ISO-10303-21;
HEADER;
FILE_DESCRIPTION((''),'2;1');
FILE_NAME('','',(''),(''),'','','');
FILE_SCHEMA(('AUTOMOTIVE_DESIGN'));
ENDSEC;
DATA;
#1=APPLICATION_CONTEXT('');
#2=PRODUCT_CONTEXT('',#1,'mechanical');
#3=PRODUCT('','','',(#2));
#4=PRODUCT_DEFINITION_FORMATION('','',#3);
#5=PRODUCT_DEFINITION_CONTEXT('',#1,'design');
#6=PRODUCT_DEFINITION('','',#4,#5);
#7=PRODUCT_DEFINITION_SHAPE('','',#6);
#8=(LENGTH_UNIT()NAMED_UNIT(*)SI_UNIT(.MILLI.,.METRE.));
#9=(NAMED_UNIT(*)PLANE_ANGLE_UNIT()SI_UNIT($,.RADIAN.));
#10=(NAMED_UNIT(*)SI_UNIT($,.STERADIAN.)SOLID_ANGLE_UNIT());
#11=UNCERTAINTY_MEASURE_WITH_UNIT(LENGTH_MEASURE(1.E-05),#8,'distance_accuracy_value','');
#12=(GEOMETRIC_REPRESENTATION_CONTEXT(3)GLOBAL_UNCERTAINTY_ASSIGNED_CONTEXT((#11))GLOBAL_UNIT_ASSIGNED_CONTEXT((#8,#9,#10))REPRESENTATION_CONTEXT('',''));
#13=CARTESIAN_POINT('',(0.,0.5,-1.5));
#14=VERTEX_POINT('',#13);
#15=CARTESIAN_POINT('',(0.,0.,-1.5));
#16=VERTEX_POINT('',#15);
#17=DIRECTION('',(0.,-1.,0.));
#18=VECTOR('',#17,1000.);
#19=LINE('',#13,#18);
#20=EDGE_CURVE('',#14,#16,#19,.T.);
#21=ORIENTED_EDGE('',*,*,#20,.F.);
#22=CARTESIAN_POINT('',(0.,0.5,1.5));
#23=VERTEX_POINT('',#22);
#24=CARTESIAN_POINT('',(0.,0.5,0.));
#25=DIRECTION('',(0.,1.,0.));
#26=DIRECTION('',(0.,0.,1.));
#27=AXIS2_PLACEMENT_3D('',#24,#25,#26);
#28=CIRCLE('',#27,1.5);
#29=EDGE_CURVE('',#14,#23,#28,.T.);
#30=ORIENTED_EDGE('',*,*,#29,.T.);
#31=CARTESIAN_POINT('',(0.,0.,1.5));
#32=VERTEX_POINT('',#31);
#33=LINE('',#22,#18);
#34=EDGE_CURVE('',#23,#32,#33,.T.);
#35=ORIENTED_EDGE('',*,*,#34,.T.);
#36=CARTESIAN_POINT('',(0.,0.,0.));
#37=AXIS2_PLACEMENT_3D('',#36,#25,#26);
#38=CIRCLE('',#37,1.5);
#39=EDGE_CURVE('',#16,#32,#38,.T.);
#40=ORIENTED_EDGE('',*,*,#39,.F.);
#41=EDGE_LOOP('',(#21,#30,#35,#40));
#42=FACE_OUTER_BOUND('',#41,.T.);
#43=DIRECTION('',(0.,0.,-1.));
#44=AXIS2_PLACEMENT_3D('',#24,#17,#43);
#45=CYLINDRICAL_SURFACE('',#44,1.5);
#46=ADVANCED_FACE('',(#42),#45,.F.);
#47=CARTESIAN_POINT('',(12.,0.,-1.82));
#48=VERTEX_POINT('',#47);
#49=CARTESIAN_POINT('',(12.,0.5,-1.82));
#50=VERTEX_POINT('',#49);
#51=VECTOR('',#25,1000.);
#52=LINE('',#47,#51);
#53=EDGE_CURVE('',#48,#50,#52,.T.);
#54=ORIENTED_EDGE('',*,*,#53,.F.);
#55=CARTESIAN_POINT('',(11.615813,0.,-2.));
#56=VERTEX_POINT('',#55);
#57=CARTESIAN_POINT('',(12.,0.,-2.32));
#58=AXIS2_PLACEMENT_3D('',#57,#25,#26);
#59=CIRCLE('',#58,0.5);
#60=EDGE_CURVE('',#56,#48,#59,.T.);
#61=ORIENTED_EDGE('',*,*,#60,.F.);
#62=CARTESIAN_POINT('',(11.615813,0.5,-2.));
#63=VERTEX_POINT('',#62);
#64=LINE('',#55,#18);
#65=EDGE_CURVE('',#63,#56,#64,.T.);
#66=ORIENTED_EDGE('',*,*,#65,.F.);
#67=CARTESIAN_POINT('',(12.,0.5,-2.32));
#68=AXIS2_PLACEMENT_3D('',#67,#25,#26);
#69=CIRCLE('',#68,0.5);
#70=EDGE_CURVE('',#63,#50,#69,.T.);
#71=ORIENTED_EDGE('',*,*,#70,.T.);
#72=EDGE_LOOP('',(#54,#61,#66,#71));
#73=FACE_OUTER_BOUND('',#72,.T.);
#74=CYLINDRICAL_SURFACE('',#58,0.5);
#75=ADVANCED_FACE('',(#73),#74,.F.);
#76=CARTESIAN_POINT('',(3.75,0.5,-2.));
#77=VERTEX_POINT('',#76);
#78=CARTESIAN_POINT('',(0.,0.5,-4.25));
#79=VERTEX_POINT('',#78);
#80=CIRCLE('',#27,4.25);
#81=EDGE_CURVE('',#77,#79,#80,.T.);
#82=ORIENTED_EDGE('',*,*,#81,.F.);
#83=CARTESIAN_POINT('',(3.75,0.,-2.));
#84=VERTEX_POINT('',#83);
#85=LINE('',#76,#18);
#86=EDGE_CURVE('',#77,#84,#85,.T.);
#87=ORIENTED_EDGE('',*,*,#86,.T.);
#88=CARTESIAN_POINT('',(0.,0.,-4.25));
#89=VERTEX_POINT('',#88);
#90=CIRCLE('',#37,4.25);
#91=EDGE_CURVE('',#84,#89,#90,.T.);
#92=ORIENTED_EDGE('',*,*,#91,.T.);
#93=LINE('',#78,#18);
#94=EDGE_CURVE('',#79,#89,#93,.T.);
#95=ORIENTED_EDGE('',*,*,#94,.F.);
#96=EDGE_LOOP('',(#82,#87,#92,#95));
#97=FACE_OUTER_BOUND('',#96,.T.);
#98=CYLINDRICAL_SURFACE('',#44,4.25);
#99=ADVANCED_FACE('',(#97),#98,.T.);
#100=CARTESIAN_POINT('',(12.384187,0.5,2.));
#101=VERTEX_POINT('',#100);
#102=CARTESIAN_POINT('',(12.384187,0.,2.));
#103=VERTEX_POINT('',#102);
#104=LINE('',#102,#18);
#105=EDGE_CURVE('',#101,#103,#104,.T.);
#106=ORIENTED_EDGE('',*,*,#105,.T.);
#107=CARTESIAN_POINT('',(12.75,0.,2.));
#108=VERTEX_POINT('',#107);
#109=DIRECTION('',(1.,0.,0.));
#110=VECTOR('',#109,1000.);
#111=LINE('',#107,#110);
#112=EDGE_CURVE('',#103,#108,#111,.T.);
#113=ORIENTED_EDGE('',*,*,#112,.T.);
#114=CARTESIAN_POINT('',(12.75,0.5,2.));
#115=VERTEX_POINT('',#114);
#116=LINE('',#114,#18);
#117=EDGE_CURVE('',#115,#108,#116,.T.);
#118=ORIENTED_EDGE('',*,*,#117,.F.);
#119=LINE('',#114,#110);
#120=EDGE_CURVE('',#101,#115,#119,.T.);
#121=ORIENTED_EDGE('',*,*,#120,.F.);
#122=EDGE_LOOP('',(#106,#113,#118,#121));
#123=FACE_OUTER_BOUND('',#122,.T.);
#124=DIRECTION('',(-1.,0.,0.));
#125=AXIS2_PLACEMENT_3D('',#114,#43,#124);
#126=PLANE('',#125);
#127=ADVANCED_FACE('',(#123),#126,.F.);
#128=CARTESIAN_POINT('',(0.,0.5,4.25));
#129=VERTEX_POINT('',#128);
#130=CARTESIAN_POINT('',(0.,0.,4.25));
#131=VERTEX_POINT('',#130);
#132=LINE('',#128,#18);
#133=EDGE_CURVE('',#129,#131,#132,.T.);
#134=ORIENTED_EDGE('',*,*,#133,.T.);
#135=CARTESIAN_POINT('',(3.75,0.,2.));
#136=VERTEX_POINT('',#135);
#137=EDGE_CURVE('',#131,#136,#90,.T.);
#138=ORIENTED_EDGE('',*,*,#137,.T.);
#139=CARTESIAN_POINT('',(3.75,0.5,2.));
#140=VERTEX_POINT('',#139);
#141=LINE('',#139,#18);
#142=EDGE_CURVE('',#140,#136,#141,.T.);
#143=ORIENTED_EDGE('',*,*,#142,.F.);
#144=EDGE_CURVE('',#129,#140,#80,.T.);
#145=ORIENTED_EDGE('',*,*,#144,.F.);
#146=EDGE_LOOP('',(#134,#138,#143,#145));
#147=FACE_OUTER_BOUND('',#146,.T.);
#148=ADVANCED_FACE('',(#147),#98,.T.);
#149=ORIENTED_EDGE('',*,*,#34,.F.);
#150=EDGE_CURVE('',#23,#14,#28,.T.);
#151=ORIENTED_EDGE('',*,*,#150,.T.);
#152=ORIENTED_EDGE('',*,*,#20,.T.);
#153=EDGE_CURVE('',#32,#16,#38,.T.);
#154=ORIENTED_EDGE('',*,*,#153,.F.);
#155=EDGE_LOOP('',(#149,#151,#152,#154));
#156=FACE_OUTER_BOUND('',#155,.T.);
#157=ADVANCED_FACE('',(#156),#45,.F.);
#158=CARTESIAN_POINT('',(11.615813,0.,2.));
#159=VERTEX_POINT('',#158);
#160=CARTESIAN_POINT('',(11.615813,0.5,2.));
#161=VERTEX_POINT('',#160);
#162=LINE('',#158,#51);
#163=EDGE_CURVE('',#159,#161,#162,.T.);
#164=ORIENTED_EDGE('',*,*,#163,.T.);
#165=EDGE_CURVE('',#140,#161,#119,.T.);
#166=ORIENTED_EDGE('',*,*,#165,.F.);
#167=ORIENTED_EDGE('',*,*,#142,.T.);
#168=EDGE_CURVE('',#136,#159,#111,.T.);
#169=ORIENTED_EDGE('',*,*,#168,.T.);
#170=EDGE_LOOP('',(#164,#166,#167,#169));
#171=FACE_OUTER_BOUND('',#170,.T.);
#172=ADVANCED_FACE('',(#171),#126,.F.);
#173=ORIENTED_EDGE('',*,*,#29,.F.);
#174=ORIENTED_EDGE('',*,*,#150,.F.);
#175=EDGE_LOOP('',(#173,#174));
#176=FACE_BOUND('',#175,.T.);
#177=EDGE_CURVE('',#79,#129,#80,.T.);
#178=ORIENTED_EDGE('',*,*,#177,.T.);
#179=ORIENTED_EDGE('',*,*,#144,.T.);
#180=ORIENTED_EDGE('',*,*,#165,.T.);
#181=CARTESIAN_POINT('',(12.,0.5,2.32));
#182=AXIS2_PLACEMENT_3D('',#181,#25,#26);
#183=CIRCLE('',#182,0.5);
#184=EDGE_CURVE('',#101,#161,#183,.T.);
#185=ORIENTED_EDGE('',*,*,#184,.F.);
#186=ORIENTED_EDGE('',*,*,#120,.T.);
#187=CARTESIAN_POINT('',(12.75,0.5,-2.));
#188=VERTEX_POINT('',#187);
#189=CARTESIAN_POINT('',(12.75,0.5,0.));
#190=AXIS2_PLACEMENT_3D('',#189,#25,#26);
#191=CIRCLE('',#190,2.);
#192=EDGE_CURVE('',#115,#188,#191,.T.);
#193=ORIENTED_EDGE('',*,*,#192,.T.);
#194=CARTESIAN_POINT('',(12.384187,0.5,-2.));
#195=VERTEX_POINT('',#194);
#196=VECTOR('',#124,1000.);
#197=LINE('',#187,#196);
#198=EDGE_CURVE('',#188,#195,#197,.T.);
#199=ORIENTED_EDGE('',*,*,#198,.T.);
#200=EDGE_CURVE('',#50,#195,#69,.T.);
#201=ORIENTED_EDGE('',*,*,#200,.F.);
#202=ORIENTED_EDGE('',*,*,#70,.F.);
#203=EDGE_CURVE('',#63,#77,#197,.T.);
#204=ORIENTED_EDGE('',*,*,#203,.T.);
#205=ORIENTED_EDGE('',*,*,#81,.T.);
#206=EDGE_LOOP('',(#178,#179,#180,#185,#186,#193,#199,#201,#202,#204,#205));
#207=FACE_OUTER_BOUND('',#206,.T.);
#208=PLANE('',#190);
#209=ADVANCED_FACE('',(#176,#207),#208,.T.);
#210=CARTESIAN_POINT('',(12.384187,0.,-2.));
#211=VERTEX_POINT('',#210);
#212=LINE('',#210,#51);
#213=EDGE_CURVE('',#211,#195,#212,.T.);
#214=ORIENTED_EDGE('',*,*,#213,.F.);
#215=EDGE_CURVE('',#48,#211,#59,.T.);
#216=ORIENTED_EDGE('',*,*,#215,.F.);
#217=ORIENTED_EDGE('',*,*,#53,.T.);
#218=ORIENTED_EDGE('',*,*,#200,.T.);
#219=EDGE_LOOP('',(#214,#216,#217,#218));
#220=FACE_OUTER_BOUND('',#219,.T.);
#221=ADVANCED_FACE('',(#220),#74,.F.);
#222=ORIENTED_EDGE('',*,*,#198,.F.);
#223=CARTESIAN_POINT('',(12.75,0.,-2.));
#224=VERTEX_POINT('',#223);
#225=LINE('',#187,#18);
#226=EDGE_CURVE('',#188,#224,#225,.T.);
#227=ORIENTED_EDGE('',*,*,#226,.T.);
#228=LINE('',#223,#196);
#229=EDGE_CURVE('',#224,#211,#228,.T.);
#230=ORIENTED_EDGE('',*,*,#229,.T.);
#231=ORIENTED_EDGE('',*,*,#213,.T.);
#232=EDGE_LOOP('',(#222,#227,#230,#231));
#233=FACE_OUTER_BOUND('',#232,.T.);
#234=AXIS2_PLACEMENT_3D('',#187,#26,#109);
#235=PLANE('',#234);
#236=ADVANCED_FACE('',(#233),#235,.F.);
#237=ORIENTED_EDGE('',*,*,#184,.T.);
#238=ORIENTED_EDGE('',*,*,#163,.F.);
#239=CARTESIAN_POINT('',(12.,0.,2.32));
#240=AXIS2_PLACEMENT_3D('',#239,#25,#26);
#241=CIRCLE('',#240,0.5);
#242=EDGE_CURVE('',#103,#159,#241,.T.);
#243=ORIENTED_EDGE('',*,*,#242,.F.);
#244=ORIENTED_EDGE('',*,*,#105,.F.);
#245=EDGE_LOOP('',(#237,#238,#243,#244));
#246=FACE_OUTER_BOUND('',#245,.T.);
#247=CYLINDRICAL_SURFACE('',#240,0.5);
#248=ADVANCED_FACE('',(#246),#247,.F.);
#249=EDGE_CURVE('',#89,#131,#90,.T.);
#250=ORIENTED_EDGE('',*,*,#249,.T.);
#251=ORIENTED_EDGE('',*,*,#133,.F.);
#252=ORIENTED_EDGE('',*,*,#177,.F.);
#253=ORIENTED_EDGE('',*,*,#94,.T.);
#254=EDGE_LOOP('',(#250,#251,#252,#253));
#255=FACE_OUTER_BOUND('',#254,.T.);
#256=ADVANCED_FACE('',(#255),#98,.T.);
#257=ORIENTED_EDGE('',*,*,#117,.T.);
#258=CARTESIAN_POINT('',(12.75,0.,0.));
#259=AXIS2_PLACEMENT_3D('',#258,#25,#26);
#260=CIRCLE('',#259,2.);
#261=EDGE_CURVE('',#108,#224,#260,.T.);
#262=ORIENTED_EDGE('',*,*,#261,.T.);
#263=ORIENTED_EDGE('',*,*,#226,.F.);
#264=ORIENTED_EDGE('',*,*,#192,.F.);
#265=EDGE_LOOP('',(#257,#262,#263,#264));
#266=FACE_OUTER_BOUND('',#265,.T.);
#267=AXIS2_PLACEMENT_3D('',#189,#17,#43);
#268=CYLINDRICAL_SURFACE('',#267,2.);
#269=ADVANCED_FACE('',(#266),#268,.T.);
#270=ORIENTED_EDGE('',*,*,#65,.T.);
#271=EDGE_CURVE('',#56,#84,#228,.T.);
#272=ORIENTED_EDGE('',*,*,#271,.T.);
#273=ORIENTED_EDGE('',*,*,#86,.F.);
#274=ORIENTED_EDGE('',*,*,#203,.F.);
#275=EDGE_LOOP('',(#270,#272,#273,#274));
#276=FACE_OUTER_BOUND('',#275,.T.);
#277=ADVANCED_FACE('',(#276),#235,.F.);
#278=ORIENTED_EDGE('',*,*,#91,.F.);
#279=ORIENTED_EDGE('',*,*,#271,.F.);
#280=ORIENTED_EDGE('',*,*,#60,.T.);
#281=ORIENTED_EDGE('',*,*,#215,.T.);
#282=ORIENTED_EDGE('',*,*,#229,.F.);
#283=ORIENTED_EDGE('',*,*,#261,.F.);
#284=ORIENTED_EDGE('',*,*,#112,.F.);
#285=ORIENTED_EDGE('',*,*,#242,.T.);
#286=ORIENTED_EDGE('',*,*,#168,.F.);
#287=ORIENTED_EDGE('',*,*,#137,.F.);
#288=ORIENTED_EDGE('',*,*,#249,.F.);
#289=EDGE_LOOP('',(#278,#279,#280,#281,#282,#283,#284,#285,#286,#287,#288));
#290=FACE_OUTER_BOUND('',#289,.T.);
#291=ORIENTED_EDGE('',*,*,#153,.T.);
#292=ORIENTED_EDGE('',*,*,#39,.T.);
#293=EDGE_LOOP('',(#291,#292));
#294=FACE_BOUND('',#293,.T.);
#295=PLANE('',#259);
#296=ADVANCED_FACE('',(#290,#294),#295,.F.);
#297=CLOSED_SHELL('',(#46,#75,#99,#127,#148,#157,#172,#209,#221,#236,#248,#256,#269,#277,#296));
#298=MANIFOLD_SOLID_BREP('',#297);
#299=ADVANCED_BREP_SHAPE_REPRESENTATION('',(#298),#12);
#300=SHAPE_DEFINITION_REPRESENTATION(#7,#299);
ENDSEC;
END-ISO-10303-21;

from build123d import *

# Parameters (mm, degrees)
SKETCH1_R           = 1.5
BOSS_EXTRUDE1_DEPTH = 0.5
SKETCH2_R           = 0.5
CUT_EXTRUDE1_DEPTH  = 16.358222553


with BuildPart() as part:
    # Sketch1 → Boss-Extrude1 (new body)
    with BuildSketch(Plane(origin=(0, 0, 0), x_dir=(1, 0, 0), z_dir=(0, 1, 0))):
        with BuildLine():
            Line((12.75, 2), (3.75, 2))
            ThreePointArc((3.75, 2), (-4.25, 0), (3.75, -2))
            Line((3.75, -2), (12.75, -2))
            ThreePointArc((12.75, -2), (14.75, 0), (12.75, 2))
        make_face()
        with Locations(Location((0, 0, 0), (0, 0, 270))):
            Circle(SKETCH1_R, mode=Mode.SUBTRACT)
    extrude(amount=BOSS_EXTRUDE1_DEPTH)

    # Sketch2 → Cut-Extrude1 (cut, through all)
    with BuildSketch(Plane(origin=(0, 0.5, 0), x_dir=(1, 0, 0), z_dir=(0, 1, 0))):
        with Locations((12, 2.32)):
            Circle(SKETCH2_R)
        with Locations((12, -2.32)):
            Circle(SKETCH2_R)
    extrude(amount=-CUT_EXTRUDE1_DEPTH, mode=Mode.SUBTRACT)


solid = part.part
